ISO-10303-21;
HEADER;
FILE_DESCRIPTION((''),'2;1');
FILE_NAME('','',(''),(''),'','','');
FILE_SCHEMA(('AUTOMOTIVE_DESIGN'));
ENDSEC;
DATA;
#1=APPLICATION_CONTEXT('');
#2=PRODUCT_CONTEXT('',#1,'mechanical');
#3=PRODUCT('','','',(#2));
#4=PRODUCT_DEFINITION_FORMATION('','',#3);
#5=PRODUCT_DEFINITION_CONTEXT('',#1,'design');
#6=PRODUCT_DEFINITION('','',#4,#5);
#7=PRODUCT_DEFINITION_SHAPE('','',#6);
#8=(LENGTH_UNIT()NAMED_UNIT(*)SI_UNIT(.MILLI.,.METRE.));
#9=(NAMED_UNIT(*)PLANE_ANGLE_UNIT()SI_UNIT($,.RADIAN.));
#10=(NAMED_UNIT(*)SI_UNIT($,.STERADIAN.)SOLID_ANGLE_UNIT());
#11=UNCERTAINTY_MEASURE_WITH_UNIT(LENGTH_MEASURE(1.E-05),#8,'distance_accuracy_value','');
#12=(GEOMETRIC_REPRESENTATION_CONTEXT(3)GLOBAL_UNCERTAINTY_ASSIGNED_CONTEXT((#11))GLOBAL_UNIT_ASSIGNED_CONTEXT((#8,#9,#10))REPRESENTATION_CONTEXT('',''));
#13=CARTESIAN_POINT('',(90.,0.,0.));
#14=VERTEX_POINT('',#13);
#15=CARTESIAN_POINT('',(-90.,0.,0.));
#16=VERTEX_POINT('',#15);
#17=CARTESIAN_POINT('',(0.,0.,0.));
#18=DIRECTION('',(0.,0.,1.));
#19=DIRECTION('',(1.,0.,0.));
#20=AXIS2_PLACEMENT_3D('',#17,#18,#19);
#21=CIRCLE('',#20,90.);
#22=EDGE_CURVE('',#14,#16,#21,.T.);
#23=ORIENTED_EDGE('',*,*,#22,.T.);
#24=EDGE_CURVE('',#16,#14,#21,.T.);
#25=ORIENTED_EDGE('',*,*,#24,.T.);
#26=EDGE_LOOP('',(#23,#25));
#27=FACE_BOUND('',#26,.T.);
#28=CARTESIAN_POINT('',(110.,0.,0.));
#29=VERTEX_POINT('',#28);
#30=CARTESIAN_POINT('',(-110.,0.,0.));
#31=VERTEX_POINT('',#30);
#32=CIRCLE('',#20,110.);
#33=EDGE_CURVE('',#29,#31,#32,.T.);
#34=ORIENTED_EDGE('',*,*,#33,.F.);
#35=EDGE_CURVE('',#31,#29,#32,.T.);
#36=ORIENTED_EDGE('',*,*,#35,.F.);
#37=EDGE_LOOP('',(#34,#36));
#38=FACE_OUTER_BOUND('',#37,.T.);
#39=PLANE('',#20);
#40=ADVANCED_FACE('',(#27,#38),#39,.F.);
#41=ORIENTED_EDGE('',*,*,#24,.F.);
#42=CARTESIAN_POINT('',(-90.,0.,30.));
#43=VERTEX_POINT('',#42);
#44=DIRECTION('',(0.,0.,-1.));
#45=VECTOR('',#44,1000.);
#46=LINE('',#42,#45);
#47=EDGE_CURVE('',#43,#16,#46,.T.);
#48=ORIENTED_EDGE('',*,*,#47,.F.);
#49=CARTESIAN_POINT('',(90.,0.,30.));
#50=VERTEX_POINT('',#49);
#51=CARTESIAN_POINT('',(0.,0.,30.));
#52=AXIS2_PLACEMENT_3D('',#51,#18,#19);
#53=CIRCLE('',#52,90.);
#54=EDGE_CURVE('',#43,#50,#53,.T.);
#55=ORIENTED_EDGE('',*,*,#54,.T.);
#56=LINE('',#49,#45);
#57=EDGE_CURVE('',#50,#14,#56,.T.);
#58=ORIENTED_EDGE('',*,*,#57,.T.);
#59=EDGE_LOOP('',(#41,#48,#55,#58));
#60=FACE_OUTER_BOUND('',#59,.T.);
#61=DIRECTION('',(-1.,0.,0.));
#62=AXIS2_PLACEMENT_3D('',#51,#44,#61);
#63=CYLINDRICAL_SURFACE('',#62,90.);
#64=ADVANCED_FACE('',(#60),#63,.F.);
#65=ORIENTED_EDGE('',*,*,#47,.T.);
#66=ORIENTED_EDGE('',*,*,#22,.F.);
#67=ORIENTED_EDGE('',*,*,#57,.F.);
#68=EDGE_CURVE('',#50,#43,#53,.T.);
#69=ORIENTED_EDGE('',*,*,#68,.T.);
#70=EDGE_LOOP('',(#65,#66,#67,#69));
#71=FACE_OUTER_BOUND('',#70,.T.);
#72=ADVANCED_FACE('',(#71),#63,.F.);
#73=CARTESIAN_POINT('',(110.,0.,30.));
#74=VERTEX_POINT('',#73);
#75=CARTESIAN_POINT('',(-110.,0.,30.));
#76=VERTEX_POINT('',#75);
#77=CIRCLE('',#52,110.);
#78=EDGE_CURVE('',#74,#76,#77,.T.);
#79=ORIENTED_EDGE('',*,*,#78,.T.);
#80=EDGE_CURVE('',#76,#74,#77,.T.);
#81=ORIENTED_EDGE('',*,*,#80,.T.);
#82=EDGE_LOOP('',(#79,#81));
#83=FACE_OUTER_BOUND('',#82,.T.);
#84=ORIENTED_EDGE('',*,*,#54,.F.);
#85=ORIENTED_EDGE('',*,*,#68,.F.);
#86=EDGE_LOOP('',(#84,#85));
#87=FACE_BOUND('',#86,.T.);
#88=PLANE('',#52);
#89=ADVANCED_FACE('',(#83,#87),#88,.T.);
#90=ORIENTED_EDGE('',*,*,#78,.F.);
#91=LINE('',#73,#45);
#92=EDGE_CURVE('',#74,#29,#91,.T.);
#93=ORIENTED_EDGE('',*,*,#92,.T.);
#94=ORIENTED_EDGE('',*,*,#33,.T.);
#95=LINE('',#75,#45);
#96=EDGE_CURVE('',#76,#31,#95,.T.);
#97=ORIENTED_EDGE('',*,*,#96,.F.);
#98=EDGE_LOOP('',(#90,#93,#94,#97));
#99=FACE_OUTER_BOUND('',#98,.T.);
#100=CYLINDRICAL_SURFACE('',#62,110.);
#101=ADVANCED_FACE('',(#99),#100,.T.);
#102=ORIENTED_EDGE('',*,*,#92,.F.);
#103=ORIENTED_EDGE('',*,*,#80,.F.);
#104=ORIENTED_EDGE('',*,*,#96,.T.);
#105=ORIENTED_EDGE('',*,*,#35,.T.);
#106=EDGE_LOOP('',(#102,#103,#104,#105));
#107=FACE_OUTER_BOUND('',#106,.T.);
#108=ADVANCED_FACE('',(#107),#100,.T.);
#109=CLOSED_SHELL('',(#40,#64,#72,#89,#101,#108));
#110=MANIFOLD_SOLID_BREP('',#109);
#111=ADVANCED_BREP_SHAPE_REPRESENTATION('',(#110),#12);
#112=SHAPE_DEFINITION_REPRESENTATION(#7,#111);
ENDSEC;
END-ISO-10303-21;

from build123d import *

# Parameters (mm, degrees)
SKETCH_1_R      = 110
SKETCH_1_R_2    = 90
EXTRUDE_2_DEPTH = 30


with BuildPart() as part:
    # 草图1 → 凸台-拉伸2 (new body)
    with BuildSketch(Plane.XY):
        Circle(SKETCH_1_R)
        Circle(SKETCH_1_R_2, mode=Mode.SUBTRACT)
    extrude(amount=EXTRUDE_2_DEPTH)


solid = part.part
